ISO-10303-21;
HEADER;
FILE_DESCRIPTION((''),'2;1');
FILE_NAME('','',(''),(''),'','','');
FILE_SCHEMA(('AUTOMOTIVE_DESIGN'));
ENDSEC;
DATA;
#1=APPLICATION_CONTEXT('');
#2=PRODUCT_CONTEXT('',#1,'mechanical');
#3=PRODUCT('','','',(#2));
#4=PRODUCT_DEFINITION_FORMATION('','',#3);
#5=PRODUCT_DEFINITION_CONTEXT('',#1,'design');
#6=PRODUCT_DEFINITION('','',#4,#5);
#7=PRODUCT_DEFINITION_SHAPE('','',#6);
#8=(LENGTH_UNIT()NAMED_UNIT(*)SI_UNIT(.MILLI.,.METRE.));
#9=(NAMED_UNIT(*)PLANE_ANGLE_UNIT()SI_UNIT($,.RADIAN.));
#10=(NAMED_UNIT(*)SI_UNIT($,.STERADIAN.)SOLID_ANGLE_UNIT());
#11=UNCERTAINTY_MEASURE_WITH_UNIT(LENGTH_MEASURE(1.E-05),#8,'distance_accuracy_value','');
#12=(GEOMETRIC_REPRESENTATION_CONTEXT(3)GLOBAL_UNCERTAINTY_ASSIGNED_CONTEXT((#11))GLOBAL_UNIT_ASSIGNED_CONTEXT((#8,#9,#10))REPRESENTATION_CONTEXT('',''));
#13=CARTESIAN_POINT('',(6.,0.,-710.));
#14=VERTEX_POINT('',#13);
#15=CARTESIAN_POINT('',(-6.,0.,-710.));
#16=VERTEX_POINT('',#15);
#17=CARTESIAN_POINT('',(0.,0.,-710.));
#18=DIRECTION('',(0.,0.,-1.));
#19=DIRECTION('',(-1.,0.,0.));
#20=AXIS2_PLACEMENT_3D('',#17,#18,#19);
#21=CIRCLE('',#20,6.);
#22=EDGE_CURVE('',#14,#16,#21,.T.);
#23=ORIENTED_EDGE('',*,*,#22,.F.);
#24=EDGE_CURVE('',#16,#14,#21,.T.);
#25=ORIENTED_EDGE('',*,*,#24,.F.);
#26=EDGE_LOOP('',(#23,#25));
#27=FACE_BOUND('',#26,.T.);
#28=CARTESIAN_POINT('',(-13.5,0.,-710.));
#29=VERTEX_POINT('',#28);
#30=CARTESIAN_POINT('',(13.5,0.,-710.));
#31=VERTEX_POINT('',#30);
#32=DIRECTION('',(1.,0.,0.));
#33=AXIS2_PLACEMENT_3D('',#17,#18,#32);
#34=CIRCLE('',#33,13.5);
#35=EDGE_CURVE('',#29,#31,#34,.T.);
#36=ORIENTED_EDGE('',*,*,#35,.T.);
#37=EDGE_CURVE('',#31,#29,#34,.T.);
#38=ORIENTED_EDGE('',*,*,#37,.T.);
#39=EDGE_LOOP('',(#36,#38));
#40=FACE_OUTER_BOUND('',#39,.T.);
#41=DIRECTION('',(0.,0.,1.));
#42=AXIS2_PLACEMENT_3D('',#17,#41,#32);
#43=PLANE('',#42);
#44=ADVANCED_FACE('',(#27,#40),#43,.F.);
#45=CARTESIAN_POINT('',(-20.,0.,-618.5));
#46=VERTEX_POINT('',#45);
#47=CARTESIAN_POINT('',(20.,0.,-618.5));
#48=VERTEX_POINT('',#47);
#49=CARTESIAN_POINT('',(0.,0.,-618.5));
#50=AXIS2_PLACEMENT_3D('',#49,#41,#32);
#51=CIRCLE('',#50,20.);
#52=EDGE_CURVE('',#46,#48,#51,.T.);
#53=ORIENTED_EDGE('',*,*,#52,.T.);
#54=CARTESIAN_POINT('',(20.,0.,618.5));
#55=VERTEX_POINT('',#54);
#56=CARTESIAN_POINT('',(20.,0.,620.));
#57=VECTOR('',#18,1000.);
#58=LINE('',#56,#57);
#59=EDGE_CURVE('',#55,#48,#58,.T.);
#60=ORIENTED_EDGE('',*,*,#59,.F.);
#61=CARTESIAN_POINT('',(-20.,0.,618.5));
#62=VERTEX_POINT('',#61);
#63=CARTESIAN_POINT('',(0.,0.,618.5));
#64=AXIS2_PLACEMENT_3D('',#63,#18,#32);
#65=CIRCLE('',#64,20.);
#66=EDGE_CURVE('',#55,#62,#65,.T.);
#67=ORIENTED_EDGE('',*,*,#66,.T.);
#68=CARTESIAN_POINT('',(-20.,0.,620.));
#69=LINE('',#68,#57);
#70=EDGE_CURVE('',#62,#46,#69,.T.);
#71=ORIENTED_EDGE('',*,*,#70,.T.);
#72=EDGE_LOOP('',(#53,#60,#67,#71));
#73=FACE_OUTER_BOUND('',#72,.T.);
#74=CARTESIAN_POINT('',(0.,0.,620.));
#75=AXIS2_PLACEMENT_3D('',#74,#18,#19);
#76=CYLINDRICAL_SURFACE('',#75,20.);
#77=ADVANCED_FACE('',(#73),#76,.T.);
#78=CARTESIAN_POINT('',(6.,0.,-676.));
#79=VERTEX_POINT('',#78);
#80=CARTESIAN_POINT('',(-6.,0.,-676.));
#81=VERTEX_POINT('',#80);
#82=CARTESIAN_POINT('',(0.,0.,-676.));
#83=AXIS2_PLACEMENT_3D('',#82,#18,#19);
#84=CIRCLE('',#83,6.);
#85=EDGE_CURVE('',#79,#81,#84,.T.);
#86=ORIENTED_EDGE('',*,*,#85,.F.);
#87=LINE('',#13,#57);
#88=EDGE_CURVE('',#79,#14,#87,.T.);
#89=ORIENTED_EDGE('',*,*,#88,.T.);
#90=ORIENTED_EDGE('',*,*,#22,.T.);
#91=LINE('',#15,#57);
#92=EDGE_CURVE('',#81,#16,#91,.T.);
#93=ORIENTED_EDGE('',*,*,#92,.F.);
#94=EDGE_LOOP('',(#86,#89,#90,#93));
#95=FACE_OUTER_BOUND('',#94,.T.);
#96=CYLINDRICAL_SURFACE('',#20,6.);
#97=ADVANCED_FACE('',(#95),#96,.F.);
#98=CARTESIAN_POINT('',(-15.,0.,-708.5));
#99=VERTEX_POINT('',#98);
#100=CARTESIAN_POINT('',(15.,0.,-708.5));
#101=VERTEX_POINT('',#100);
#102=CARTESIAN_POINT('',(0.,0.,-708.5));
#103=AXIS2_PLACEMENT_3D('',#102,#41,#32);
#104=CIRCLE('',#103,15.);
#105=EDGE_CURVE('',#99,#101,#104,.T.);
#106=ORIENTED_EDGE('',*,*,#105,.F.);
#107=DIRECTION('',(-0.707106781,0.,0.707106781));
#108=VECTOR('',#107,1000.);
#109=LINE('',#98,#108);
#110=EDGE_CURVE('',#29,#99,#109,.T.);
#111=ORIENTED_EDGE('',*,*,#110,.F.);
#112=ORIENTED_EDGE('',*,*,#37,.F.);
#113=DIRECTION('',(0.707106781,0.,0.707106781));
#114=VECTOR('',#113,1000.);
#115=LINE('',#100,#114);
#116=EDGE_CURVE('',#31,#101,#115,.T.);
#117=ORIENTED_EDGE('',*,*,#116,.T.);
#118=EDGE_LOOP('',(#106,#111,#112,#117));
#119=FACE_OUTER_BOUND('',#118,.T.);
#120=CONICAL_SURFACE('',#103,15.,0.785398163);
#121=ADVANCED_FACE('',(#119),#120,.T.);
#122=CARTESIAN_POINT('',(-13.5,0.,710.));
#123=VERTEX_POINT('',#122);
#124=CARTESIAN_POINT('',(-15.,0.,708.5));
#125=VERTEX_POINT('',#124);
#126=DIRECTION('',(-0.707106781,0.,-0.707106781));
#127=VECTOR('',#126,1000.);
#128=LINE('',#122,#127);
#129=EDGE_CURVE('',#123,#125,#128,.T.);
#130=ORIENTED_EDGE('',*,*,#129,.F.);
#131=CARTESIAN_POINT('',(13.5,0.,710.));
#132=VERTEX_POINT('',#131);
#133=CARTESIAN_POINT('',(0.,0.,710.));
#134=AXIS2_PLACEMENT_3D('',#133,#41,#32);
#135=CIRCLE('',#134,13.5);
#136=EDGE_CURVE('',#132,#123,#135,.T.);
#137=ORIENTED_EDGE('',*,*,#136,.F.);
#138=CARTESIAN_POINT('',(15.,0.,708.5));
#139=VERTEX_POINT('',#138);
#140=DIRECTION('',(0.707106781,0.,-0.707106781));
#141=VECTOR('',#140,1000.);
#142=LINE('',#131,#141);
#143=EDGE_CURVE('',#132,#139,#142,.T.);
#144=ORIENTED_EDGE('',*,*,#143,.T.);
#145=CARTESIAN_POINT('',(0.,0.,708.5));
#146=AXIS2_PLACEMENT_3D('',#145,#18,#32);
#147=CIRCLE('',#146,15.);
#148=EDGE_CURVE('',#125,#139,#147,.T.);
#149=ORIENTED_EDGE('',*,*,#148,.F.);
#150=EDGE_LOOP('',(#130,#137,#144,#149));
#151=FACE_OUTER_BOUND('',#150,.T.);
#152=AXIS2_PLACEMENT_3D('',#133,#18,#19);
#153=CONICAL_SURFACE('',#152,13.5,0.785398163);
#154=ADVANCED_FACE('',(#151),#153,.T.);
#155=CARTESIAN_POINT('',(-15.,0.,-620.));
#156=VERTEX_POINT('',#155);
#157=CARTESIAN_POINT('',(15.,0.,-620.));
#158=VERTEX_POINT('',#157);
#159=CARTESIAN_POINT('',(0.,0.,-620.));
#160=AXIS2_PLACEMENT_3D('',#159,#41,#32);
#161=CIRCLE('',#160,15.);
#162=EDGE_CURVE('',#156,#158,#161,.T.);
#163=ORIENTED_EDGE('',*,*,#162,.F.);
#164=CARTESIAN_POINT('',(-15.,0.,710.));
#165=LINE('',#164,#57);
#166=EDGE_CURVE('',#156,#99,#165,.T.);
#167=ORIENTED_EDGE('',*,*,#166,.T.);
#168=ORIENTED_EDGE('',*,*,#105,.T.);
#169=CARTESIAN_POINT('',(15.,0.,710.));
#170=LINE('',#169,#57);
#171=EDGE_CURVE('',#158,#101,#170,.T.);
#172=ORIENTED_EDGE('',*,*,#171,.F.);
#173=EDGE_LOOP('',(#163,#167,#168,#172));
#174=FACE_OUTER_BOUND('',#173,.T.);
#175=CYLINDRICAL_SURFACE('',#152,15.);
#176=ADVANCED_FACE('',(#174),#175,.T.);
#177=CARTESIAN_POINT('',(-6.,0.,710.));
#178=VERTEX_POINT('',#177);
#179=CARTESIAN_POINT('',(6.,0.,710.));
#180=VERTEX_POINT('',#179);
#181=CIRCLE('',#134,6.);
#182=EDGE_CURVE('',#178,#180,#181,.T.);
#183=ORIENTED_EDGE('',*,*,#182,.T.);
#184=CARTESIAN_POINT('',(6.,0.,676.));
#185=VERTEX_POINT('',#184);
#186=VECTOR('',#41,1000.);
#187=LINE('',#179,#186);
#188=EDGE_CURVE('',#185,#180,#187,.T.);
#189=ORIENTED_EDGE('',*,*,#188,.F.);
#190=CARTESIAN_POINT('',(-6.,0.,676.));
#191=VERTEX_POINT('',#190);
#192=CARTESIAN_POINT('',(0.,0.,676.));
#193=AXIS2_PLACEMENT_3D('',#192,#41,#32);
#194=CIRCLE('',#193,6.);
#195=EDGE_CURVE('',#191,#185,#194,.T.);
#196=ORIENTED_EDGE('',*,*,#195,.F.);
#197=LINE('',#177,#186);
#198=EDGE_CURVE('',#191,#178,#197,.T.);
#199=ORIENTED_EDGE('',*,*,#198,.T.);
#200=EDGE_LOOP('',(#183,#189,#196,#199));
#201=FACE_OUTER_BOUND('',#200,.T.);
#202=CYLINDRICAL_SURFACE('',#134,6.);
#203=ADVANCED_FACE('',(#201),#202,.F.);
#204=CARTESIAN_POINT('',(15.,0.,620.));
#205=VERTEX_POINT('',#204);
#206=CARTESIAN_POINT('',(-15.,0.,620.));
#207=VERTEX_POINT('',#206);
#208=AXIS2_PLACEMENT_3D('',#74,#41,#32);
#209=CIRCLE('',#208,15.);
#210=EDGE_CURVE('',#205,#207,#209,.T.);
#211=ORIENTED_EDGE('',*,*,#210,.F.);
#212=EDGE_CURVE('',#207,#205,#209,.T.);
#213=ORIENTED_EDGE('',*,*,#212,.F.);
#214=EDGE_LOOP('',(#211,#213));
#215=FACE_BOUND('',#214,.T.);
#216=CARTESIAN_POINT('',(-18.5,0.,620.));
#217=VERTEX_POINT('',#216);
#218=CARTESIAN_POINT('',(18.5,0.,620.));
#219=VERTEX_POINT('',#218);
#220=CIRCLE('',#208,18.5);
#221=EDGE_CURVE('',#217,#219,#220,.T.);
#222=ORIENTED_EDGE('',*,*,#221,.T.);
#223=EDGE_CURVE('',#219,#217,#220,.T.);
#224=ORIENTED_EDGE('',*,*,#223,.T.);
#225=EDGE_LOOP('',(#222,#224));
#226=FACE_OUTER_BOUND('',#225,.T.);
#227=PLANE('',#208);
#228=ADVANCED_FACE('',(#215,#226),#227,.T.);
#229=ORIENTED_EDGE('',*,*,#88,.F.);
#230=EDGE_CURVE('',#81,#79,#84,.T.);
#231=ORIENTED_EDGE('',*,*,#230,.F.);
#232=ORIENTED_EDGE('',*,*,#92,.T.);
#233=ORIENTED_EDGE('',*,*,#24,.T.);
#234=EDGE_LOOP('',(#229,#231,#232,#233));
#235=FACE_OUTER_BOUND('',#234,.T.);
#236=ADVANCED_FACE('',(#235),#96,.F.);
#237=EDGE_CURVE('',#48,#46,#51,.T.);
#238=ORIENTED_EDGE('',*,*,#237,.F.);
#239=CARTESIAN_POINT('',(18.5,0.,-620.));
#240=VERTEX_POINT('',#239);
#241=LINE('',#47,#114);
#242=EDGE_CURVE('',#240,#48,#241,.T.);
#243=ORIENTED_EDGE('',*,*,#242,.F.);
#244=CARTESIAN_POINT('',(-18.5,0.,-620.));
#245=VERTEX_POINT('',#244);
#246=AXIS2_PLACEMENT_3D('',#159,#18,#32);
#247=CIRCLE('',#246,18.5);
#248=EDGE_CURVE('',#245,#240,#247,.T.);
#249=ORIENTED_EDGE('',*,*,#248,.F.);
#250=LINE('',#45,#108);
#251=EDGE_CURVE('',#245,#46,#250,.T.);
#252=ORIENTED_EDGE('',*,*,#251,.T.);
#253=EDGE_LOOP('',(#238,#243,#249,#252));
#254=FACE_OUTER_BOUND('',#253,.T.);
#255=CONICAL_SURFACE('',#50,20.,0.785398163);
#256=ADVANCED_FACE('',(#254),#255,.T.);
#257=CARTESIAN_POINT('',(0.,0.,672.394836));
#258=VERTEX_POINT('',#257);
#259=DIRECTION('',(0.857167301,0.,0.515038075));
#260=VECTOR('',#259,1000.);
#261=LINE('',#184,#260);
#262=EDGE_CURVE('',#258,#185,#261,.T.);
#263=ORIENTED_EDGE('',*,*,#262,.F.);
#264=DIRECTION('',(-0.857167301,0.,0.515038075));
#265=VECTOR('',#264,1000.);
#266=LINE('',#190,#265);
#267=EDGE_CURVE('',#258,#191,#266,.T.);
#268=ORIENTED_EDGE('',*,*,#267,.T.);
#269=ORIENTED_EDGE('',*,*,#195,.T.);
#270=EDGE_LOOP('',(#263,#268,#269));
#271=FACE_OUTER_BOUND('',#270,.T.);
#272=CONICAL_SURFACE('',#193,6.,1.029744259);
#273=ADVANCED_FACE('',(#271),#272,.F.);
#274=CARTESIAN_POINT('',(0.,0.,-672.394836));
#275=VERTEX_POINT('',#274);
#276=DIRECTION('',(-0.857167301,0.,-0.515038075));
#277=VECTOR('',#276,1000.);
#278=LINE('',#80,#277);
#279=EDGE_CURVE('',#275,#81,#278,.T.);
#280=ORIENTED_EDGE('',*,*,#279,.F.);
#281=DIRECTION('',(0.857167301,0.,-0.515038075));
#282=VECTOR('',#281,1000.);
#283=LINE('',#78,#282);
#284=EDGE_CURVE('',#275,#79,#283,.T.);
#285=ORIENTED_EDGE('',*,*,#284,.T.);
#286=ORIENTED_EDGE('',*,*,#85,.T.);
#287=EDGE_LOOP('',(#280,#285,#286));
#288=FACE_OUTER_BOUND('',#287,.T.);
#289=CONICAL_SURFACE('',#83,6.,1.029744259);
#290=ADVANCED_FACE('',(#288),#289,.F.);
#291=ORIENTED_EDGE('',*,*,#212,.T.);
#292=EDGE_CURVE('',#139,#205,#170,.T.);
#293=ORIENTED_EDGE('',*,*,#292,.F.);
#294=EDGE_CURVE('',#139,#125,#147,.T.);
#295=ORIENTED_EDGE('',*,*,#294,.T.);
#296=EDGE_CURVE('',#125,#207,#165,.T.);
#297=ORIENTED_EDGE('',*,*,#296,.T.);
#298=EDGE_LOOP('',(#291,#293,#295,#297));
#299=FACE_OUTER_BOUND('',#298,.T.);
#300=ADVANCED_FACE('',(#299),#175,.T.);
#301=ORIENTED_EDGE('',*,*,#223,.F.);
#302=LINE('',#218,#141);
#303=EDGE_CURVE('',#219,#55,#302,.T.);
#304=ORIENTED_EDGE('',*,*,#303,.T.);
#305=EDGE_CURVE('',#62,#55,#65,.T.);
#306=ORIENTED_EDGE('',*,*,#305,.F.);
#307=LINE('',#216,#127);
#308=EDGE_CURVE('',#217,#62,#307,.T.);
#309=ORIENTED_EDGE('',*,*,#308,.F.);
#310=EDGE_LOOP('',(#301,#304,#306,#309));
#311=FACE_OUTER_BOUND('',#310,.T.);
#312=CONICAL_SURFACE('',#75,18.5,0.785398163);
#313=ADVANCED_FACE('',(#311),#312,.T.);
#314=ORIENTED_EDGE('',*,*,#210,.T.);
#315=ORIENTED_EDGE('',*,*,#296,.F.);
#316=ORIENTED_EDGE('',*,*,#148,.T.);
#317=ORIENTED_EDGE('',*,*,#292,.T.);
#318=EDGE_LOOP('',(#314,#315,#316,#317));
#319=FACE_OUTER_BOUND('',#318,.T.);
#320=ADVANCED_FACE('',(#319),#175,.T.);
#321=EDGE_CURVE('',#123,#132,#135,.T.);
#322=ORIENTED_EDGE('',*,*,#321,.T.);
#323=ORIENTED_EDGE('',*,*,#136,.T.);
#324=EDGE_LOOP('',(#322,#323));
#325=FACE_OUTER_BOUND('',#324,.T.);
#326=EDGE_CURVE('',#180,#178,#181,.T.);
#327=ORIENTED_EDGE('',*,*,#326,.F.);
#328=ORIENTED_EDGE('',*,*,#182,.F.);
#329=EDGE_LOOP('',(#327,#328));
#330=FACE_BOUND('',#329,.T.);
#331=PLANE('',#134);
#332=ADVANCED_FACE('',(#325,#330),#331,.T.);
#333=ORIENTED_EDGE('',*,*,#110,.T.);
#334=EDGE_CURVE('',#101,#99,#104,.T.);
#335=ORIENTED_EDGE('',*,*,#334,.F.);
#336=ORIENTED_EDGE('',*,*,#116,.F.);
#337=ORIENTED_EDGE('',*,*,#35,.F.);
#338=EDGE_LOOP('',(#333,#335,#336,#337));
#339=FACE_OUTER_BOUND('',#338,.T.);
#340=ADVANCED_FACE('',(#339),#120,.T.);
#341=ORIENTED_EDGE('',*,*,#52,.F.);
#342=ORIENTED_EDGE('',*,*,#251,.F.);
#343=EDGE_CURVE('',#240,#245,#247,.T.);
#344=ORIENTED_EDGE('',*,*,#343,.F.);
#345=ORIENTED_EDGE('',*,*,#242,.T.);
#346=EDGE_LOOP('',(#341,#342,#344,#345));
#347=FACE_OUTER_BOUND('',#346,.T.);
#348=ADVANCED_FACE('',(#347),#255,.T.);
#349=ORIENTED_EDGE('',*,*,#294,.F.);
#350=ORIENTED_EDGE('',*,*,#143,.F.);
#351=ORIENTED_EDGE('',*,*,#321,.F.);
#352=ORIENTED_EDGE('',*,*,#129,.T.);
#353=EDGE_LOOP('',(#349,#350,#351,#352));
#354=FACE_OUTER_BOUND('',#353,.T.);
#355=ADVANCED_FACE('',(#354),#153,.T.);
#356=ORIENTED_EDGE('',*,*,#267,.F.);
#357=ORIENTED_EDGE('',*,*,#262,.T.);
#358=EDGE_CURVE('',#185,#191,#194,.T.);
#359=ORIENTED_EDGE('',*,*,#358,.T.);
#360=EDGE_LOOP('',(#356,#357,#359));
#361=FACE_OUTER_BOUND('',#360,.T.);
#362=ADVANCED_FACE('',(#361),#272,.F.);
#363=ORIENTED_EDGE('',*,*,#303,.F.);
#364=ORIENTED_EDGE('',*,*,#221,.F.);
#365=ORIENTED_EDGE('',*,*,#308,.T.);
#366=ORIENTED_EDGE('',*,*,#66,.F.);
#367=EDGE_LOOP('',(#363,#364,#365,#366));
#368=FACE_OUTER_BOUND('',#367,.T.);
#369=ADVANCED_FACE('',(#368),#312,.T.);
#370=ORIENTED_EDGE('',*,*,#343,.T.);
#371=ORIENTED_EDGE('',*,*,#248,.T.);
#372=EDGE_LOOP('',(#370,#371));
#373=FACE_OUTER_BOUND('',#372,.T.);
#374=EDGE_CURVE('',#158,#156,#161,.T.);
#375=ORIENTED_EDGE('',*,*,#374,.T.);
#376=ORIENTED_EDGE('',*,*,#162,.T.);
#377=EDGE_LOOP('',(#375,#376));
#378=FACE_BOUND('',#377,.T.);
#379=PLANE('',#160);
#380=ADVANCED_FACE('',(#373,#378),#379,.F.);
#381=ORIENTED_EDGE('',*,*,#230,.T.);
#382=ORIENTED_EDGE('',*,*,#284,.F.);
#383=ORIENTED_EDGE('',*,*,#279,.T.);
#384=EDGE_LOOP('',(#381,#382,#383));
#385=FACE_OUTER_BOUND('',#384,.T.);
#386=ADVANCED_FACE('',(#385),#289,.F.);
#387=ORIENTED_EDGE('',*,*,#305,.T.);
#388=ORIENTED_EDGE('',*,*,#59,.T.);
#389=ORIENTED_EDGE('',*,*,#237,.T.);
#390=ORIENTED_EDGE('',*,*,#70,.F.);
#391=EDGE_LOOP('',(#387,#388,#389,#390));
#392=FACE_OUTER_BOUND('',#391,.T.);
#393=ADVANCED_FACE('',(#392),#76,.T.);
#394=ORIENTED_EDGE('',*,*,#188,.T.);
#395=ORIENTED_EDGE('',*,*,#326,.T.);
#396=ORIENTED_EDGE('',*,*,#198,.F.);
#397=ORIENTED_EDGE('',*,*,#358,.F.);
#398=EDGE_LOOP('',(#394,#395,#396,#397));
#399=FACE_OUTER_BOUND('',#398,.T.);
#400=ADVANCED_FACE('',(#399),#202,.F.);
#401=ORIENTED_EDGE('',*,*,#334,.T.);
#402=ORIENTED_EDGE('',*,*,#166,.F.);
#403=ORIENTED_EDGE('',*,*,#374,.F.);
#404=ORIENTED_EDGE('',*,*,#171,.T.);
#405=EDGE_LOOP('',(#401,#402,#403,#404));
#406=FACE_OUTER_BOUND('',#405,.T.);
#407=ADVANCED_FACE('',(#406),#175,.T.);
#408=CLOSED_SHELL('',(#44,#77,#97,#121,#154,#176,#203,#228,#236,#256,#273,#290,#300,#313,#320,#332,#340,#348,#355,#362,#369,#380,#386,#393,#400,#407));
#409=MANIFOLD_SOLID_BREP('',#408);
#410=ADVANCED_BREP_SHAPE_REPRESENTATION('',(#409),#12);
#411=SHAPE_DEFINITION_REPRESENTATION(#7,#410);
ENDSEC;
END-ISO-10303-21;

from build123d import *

# Parameters (mm, degrees)
SKETCH1_R              = 15
BOSS_EXTRUDE1_DEPTH    = 710
M14_TAPPED_HOLE2_D     = 12
M14_TAPPED_HOLE2_DEPTH = 34
M14_TAPPED_HOLE2_TIP   = 3.605163714
M14_TAPPED_HOLE1_D     = 12
M14_TAPPED_HOLE1_DEPTH = 34
M14_TAPPED_HOLE1_TIP   = 3.605163714
SKETCH7_R              = 20
BOSS_EXTRUDE3_DEPTH    = 620
CHAMFER1_SIZE          = 1.5


with BuildPart() as part:
    # Sketch1 → Boss-Extrude1 (new, symmetric)
    with BuildSketch(Plane.XY):
        Circle(SKETCH1_R)
    extrude(amount=BOSS_EXTRUDE1_DEPTH, both=True)

    # M14 Tapped Hole2
    with Locations(Plane.XY.offset(710)):
        with Locations((0, 0)):
            Hole(M14_TAPPED_HOLE2_D / 2, depth=M14_TAPPED_HOLE2_DEPTH)
            with Locations((0, 0, -(M14_TAPPED_HOLE2_DEPTH + M14_TAPPED_HOLE2_TIP / 2))):  # 118° drill point
                Cone(0, M14_TAPPED_HOLE2_D / 2, M14_TAPPED_HOLE2_TIP, mode=Mode.SUBTRACT)

    # M14 Tapped Hole1
    with Locations(Plane(origin=(0, 0, -710), x_dir=(-1, 0, 0), z_dir=(0, 0, -1))):
        with Locations((0, 0)):
            Hole(M14_TAPPED_HOLE1_D / 2, depth=M14_TAPPED_HOLE1_DEPTH)
            with Locations((0, 0, -(M14_TAPPED_HOLE1_DEPTH + M14_TAPPED_HOLE1_TIP / 2))):  # 118° drill point
                Cone(0, M14_TAPPED_HOLE1_D / 2, M14_TAPPED_HOLE1_TIP, mode=Mode.SUBTRACT)

    # Sketch7 → Boss-Extrude3 (add, symmetric)
    with BuildSketch(Plane.XY):
        Circle(SKETCH7_R)
    extrude(amount=BOSS_EXTRUDE3_DEPTH, both=True)

    # Chamfer1
    chamfer1_edges = [part.edges().sort_by_distance(p)[0] for p in [
        (-20, 0, -620),
        (-20, 0, 620),
        (-15, 0, -710),
        (-15, 0, 710),
    ]]
    chamfer(chamfer1_edges, length=CHAMFER1_SIZE)


solid = part.part
